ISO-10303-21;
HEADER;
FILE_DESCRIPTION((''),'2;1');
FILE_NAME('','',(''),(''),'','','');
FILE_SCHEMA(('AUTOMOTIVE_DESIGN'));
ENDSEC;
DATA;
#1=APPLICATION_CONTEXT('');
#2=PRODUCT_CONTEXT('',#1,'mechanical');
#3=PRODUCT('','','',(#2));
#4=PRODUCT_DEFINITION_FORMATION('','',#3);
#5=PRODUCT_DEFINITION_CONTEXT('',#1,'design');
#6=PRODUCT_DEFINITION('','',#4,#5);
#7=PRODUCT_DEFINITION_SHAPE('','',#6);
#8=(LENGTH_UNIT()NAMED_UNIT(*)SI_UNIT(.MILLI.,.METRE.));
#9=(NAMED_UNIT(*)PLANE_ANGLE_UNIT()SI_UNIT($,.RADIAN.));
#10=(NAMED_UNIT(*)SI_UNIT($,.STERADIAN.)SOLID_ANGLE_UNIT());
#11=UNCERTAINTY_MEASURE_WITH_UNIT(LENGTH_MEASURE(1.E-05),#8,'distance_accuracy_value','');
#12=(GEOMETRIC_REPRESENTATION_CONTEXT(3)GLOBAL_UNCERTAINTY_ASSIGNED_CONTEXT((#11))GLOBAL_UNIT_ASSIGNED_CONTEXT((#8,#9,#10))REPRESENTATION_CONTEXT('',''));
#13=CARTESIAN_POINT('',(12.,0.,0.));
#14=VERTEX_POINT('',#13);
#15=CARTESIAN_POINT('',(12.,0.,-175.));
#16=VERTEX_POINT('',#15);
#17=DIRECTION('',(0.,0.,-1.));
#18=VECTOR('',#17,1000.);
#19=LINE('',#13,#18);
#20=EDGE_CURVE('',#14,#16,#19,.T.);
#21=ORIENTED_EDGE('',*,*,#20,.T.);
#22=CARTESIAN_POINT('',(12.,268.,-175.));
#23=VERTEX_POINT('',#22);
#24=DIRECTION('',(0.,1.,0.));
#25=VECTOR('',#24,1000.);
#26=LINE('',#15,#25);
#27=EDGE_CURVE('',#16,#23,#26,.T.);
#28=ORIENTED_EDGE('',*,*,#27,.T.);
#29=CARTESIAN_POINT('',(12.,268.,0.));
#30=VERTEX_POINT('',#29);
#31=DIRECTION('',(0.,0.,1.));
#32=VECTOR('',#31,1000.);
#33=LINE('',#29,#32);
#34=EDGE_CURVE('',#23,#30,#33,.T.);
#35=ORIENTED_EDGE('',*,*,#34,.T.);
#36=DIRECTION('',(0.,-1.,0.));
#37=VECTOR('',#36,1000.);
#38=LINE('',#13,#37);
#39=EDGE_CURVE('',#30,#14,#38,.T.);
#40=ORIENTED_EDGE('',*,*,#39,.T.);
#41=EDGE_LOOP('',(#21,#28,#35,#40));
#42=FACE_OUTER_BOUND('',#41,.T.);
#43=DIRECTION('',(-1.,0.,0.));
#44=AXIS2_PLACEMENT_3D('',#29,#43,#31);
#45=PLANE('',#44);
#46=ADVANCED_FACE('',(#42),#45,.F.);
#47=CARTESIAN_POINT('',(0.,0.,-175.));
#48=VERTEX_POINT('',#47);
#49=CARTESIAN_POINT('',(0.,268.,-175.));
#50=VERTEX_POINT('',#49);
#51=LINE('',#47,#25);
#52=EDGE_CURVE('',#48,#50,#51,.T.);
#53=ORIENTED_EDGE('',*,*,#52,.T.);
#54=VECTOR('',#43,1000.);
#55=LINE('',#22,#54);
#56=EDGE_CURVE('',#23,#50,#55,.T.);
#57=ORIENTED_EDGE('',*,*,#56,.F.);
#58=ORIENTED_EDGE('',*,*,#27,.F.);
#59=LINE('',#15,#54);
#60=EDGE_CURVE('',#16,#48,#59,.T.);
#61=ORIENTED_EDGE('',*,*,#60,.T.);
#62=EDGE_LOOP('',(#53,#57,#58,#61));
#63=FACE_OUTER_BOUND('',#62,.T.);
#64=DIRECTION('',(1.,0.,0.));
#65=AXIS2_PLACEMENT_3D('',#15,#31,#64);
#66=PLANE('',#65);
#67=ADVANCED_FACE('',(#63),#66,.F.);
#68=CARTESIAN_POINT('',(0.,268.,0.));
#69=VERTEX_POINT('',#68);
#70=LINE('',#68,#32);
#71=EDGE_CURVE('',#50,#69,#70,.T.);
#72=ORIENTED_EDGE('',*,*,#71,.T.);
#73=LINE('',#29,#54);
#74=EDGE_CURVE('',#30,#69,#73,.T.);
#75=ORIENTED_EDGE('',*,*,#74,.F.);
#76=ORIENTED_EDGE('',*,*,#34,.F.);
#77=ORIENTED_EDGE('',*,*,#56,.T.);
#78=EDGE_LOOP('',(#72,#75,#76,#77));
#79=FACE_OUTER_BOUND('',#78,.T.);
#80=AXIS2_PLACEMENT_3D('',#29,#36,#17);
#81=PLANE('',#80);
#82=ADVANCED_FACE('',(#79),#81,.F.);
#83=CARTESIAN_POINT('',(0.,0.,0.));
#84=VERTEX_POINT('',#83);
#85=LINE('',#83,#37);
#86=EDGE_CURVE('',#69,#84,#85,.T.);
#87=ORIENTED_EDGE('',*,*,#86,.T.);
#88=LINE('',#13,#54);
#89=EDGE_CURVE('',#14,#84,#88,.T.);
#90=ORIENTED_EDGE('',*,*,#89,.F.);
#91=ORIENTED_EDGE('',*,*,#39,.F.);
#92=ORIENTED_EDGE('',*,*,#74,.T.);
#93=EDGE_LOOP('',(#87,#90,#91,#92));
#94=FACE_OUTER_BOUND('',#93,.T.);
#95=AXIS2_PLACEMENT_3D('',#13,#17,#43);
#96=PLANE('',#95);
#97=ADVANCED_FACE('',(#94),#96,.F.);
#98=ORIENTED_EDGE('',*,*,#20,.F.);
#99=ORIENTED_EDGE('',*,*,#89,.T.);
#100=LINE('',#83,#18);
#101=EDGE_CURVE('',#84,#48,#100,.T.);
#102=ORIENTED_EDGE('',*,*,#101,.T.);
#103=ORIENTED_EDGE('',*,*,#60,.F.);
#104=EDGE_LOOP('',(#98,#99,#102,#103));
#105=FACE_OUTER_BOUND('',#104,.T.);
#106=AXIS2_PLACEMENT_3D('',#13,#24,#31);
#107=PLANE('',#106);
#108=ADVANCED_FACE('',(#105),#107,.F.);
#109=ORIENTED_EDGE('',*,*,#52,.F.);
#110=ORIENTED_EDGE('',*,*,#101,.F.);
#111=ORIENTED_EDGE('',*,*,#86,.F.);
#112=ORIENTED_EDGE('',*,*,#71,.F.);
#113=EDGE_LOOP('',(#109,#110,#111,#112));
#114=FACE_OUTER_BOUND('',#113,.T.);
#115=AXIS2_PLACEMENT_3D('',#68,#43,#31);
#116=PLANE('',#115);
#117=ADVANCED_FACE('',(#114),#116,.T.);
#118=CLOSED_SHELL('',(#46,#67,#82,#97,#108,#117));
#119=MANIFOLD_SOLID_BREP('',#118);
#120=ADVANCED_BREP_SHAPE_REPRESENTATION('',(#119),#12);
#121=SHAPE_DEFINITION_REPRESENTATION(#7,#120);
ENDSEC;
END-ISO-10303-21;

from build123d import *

# Parameters (mm, degrees)
SKETCH1_W           = 175
SKETCH1_H           = 268
BOSS_EXTRUDE1_DEPTH = 12


with BuildPart() as part:
    # Sketch1 → Boss-Extrude1 (new body)
    with BuildSketch(Plane(origin=(0, 0, 0), x_dir=(0, 0, -1), z_dir=(1, 0, 0))):
        with Locations((87.5, 134)):
            Rectangle(SKETCH1_W, SKETCH1_H)
    extrude(amount=BOSS_EXTRUDE1_DEPTH)


solid = part.part
